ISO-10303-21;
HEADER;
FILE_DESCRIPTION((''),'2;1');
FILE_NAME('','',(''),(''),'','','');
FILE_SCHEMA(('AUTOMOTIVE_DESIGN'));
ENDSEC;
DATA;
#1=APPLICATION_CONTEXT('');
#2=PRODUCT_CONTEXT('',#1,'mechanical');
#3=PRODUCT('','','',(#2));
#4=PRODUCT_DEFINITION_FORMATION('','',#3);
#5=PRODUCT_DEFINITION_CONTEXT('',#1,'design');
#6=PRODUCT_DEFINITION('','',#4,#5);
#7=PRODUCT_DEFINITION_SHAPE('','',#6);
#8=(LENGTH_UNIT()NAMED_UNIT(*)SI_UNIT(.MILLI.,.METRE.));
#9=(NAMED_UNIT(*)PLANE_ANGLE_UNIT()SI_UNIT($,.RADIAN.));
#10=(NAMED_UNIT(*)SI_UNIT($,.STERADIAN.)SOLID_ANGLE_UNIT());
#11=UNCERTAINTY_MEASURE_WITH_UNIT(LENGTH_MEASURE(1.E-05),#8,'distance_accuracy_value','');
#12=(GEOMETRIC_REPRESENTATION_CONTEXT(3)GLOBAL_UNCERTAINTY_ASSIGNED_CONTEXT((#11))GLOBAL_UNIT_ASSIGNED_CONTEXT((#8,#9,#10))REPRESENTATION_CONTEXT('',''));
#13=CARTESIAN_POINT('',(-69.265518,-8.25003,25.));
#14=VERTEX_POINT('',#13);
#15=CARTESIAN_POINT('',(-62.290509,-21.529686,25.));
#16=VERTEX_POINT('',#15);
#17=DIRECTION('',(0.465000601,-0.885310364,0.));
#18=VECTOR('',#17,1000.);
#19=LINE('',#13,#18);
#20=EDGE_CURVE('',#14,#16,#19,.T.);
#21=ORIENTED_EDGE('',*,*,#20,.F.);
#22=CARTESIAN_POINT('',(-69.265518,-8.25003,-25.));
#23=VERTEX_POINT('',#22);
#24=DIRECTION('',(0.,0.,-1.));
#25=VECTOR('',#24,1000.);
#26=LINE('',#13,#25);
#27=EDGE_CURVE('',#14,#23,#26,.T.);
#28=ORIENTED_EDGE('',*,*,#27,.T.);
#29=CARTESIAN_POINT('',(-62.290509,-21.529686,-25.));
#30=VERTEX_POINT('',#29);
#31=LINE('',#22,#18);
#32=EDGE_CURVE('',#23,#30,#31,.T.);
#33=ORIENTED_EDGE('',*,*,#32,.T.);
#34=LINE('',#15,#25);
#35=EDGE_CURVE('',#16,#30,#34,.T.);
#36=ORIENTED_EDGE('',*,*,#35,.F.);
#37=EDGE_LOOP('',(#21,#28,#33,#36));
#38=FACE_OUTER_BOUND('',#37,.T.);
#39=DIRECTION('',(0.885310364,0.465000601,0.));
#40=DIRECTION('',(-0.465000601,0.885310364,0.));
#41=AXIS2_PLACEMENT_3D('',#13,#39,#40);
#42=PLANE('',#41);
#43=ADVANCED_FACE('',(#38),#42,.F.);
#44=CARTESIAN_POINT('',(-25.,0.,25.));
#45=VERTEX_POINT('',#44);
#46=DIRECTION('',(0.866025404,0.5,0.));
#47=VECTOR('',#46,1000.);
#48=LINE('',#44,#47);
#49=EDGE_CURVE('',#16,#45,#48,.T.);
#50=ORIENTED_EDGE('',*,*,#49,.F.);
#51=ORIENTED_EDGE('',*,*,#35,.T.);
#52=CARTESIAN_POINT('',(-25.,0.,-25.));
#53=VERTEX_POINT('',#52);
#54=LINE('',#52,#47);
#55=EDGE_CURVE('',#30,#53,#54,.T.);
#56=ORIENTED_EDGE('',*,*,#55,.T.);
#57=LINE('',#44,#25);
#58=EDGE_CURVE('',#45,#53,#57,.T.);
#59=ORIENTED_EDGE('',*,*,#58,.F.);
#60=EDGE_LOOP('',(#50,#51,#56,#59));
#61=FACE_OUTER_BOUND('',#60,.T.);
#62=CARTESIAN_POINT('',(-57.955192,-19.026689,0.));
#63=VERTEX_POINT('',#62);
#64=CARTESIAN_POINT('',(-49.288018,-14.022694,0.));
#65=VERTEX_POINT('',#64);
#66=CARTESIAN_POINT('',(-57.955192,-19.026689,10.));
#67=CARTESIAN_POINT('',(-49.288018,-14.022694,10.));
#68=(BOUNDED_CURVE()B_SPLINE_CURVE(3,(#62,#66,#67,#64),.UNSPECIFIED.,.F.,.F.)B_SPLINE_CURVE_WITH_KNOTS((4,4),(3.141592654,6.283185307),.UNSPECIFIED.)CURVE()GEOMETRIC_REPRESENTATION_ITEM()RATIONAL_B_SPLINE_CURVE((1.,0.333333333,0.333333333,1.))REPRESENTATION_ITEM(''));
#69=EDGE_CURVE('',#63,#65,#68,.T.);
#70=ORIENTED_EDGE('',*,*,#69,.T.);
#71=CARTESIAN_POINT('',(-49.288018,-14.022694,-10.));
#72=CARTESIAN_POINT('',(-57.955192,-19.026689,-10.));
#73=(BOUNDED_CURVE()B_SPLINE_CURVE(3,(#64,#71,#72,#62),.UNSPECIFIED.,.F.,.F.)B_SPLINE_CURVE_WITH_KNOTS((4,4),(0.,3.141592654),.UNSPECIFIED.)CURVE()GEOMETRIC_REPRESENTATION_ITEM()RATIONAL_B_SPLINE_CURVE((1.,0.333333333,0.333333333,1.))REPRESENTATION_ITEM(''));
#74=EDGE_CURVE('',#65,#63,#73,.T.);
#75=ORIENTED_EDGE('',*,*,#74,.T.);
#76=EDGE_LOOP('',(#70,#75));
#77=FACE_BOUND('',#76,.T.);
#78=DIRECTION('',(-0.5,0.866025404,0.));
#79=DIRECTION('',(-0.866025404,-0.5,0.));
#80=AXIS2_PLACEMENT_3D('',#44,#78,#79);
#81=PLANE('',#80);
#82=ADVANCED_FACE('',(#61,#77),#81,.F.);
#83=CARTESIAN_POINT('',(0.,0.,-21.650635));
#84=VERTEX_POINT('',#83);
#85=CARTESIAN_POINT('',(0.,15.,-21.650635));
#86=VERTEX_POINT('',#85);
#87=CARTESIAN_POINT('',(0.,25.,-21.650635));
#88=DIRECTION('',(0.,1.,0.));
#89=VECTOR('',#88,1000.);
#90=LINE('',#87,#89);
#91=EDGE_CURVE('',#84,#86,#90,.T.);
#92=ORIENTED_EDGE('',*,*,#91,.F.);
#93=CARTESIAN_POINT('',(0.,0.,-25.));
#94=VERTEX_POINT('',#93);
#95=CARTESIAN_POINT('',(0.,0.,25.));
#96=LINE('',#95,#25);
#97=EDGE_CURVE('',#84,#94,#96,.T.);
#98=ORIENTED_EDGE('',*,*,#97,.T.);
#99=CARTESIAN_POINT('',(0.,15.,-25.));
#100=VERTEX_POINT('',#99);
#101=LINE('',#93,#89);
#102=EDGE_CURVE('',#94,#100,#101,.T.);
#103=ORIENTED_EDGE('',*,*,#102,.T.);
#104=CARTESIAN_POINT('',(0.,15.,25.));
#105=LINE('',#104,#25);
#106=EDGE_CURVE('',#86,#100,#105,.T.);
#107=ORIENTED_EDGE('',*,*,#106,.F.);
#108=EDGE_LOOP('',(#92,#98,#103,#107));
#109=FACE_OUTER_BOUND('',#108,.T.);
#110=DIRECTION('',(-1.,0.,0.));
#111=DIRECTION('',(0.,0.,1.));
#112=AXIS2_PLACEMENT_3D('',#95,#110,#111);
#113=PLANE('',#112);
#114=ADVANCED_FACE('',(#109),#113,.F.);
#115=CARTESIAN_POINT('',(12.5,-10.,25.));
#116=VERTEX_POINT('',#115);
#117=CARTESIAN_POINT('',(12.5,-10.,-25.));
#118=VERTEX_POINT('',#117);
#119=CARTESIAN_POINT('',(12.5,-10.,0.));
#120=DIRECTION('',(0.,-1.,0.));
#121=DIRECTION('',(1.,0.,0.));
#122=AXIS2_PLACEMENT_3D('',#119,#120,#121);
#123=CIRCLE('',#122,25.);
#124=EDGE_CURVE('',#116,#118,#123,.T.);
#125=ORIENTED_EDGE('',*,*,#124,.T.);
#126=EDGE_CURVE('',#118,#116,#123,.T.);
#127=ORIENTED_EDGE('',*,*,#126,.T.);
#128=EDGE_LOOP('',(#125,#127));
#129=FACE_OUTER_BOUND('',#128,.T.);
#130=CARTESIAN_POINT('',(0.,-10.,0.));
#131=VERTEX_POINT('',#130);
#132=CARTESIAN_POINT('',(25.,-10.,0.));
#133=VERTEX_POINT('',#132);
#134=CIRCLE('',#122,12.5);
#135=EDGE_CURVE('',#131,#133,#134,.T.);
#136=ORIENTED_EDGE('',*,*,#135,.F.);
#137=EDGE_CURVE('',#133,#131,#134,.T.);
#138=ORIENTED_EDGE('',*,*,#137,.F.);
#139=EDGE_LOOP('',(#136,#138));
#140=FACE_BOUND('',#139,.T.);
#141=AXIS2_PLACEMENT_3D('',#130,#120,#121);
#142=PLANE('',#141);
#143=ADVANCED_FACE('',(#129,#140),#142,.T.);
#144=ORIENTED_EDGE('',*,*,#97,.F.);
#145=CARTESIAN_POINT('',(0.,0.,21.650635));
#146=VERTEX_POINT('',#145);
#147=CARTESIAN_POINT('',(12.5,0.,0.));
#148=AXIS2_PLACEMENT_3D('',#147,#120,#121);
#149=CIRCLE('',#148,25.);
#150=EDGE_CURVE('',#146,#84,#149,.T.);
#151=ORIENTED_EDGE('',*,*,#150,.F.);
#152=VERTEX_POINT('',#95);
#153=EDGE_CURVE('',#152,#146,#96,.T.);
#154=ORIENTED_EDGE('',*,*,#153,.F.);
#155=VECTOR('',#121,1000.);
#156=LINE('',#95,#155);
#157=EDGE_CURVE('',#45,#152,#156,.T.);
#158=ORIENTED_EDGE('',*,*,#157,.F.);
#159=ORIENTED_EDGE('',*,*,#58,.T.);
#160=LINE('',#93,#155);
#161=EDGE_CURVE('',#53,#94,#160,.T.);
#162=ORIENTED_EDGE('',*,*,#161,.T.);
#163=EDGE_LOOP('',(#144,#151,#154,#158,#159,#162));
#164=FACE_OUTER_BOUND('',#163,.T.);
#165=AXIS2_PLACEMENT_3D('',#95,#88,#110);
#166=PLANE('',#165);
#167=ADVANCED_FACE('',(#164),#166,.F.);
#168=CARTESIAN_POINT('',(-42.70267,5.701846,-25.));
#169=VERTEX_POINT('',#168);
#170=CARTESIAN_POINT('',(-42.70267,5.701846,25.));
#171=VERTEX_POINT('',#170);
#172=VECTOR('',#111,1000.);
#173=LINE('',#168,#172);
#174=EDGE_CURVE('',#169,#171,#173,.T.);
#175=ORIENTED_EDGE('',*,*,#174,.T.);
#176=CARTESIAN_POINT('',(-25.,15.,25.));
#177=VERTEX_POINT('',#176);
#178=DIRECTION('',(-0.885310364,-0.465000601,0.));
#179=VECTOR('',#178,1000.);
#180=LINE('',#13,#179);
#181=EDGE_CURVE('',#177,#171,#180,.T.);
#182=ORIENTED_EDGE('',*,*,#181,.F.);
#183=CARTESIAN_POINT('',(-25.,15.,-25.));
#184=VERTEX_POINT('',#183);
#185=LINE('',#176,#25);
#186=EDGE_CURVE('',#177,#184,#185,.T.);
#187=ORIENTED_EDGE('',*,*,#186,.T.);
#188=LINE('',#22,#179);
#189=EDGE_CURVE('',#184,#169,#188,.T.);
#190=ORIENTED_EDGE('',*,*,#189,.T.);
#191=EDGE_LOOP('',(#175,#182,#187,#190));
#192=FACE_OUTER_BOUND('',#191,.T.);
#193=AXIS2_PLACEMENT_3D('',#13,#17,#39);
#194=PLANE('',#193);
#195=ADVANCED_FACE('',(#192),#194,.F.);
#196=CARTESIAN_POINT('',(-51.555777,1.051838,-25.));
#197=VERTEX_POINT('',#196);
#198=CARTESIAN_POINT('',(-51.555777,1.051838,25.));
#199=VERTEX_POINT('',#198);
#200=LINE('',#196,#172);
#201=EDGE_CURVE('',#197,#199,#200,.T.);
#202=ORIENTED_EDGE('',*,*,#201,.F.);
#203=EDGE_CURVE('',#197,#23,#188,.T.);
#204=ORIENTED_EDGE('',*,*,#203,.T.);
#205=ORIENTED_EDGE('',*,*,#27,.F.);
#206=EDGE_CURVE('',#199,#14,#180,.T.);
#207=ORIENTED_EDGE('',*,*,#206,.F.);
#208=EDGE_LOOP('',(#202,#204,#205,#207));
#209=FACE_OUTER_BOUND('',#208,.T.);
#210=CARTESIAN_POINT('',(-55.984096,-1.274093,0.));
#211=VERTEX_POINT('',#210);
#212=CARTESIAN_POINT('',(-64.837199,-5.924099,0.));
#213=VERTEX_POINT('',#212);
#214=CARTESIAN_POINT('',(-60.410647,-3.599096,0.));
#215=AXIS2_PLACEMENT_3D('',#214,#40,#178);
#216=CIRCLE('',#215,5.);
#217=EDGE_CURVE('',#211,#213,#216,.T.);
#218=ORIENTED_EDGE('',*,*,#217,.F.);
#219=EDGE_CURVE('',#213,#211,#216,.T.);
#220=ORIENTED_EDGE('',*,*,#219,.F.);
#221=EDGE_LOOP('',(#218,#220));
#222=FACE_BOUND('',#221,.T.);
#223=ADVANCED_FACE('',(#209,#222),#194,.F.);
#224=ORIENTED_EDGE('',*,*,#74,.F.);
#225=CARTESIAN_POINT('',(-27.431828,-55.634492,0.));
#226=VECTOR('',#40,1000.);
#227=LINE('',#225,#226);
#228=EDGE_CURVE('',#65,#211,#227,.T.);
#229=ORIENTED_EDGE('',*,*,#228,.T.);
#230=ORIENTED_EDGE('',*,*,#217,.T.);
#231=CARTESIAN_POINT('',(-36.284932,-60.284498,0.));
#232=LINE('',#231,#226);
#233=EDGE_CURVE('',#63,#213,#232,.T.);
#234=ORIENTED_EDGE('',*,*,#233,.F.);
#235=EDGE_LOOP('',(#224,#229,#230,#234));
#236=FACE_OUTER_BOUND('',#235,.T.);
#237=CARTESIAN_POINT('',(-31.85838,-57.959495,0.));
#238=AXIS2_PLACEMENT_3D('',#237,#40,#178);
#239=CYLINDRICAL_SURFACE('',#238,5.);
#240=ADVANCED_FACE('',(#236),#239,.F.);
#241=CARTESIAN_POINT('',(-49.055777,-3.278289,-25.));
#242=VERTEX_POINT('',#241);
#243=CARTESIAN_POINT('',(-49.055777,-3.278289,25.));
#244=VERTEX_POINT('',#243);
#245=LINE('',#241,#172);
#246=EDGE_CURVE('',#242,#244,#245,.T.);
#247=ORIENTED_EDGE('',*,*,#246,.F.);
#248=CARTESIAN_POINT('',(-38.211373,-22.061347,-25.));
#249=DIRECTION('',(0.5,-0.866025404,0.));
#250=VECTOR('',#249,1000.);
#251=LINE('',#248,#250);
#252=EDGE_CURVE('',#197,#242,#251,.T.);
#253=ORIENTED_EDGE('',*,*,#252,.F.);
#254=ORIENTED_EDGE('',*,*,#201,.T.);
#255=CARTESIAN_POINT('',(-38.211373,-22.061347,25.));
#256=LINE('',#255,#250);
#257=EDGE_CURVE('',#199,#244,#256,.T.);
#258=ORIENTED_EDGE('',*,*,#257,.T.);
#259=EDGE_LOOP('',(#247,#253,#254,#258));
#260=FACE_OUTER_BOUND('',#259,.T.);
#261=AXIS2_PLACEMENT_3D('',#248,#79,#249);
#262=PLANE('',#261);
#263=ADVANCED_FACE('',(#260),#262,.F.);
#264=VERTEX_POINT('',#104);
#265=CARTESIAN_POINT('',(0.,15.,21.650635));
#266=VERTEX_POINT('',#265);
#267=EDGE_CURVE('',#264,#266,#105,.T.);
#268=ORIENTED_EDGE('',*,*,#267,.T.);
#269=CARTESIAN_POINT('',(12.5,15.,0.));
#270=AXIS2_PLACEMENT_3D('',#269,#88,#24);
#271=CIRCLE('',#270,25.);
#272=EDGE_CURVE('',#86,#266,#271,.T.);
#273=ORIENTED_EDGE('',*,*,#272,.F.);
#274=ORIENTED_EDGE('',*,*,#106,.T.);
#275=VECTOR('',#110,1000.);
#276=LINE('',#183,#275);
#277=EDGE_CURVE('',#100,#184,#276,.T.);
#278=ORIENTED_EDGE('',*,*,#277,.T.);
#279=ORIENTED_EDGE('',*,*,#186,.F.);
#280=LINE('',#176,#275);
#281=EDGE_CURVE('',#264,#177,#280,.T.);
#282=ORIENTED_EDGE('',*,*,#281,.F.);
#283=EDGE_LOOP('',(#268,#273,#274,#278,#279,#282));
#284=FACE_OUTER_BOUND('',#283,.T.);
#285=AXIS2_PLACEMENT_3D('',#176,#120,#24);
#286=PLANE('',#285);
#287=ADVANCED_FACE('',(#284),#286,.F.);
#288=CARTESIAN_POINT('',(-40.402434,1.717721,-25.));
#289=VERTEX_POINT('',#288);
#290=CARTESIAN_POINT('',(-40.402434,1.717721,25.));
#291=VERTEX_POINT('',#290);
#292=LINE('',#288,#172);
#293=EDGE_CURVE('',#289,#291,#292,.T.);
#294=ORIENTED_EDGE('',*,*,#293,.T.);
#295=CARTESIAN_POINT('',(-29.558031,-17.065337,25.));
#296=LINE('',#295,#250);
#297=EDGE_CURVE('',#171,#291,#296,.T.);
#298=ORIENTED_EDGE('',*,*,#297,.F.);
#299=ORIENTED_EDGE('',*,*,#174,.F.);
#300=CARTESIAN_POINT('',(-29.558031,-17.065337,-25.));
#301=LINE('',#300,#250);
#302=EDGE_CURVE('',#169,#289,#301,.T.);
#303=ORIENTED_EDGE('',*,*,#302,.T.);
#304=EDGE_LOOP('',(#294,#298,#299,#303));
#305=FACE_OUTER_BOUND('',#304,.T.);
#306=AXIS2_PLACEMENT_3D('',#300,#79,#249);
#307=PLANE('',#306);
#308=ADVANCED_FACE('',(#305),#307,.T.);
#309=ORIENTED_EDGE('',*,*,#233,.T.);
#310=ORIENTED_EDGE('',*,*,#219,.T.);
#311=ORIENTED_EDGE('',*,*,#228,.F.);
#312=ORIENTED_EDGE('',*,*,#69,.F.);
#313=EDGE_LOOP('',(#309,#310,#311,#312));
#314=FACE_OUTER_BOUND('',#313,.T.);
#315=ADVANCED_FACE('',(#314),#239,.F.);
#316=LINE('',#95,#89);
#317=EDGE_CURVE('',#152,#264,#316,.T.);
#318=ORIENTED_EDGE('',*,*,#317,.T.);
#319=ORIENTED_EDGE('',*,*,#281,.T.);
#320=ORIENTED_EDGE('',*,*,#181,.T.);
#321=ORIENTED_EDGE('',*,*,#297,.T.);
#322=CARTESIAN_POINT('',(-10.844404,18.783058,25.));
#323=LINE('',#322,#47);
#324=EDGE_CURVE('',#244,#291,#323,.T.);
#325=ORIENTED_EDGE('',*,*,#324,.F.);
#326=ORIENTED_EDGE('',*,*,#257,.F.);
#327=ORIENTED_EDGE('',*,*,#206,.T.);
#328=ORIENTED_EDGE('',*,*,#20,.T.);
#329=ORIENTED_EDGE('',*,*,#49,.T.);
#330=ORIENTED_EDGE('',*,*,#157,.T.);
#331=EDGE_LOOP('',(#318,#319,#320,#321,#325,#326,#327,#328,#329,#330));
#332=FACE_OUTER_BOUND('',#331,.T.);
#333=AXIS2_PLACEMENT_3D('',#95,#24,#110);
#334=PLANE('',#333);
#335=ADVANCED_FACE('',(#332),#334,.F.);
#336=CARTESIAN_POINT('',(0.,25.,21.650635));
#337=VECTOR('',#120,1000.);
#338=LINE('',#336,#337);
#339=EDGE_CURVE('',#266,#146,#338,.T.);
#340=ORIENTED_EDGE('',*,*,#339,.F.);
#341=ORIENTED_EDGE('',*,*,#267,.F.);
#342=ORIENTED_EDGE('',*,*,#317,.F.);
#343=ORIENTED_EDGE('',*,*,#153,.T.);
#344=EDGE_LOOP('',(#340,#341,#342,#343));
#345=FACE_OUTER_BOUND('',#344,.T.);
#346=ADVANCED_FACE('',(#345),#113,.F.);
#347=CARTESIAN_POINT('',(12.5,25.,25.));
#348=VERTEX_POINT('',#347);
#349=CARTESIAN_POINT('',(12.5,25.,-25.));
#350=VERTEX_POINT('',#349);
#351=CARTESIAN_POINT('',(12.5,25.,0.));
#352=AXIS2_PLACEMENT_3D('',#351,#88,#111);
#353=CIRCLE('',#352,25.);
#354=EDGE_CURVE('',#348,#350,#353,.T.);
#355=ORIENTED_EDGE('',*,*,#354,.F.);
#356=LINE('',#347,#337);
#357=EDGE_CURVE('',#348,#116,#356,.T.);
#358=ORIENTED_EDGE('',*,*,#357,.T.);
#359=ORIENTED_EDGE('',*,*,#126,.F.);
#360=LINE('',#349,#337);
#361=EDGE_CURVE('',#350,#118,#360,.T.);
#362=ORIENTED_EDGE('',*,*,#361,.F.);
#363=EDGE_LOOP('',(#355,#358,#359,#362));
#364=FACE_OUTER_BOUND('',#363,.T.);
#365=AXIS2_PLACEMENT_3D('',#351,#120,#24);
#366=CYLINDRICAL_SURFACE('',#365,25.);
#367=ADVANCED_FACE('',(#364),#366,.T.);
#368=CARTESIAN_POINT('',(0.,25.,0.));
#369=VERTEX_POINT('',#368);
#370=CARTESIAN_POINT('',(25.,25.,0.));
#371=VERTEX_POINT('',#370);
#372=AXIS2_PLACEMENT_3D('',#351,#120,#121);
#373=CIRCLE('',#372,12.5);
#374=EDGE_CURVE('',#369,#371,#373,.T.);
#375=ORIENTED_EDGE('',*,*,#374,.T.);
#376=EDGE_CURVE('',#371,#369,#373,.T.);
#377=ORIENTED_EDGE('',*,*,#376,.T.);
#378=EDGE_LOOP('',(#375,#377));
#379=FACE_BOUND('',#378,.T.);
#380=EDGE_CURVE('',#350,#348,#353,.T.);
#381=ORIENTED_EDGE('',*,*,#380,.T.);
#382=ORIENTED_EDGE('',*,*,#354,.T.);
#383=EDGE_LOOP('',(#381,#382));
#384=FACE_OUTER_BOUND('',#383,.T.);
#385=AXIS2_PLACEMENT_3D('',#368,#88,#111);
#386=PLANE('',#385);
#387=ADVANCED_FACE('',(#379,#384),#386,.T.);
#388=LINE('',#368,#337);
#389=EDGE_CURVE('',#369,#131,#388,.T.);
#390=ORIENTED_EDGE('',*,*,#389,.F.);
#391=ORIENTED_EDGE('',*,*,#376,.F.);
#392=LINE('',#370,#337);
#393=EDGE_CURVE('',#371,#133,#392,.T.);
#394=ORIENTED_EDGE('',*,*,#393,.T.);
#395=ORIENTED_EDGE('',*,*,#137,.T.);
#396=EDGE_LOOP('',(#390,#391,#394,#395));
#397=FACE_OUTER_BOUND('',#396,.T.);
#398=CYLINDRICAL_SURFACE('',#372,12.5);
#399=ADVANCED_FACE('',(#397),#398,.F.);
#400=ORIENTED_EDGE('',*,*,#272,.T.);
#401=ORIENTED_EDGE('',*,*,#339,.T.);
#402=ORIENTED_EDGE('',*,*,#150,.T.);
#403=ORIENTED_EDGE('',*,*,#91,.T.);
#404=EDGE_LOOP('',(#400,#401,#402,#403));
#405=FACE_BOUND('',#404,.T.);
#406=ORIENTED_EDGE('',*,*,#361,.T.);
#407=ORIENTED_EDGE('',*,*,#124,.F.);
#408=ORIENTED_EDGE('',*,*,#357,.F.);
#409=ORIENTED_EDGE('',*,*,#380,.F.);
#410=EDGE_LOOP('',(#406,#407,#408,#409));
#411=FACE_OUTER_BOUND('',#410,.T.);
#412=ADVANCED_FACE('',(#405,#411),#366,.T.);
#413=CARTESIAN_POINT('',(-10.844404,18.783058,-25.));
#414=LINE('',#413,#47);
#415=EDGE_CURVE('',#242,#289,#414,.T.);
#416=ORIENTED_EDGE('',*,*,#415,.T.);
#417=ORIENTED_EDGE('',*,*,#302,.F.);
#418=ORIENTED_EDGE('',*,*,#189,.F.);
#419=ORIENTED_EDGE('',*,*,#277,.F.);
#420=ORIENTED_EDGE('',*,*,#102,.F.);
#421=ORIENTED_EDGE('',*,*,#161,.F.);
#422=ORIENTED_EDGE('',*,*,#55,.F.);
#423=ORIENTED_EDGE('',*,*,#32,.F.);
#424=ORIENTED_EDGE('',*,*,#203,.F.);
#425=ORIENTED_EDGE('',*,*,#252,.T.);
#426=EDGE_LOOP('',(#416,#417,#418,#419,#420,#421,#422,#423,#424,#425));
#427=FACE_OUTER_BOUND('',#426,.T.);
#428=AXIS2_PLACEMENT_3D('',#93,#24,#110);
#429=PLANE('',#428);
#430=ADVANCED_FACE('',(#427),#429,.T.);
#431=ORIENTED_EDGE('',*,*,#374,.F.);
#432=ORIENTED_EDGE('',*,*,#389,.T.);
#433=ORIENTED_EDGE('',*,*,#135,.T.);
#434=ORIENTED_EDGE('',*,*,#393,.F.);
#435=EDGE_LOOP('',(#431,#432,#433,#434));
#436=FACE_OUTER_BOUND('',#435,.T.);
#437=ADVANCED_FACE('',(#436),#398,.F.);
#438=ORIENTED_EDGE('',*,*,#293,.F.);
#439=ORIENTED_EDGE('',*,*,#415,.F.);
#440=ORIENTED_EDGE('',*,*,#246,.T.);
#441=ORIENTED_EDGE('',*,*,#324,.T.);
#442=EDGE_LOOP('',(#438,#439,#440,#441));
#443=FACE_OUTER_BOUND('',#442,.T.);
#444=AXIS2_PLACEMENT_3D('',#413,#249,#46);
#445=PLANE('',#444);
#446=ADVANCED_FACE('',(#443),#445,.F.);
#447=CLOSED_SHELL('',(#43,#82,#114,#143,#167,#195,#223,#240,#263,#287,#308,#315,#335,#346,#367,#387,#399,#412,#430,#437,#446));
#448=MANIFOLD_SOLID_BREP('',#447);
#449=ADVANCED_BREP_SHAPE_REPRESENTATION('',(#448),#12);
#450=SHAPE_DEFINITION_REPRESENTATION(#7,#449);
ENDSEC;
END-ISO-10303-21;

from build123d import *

# Parameters (mm, degrees)
BASE_BLOCK_DEPTH       = 25
CYLINDER_BOSS_SKETCH_R = 25
CYLINDER_BOSS_50_DEPTH = 25
WEB_START              = 10
WEB_BOSS_DEPTH         = 10
BORE_SKETCH_R          = 12.5
BORE_25_DEPTH          = 82.533502
T_SLOT_CUT_DEPTH       = 90.009618
HOLE_SKETCH_R          = 5
HOLE_10_DEPTH          = 77.495661


with BuildPart() as part:
    # Base Profile Sketch → Base Block (new, symmetric)
    with BuildSketch(Plane.XY):
        Polygon((0, 0), (-25, 0), (-62.290509, -21.529686), (-69.265518, -8.25003), (-25, 15), (0, 15), align=None)
    extrude(amount=BASE_BLOCK_DEPTH, both=True)

    # Cylinder Boss Sketch → Cylinder Boss Ø50 (add)
    with BuildSketch(Plane(origin=(0, 0, 0), x_dir=(1, 0, 0), z_dir=(0, 1, 0))):
        with Locations(Location((12.5, 0, 0), (0, 0, 120))):
            Circle(CYLINDER_BOSS_SKETCH_R)
    extrude(amount=CYLINDER_BOSS_50_DEPTH)

    # Web Boss Sketch → Web Boss (add)
    with BuildSketch(Plane.XZ.offset(WEB_START)):
        with BuildLine():
            ThreePointArc((0, 21.650635), (-12.5, 0), (0, -21.650635))
            ThreePointArc((0, -21.650635), (25, -21.650635), (37.5, 0))
            ThreePointArc((37.5, 0), (25, 21.650635), (0, 21.650635))
        make_face()
    extrude(amount=-WEB_BOSS_DEPTH)

    # Bore Sketch → Bore Ø25 (cut, through all)
    with BuildSketch(Plane.XZ.offset(10)):
        with Locations((12.5, 0)):
            Circle(BORE_SKETCH_R)
    extrude(amount=-BORE_25_DEPTH, mode=Mode.SUBTRACT)

    # T-Slot Sketch → T-Slot Cut (cut, through all)
    with BuildSketch(Plane.XY.offset(25)):
        Polygon((-42.70267, 5.701846), (-51.555777, 1.051838), (-49.055777, -3.278289), (-40.402434, 1.717721), align=None)
    extrude(amount=-T_SLOT_CUT_DEPTH, mode=Mode.SUBTRACT)

    # Hole Sketch → Hole Ø10 (cut, through all)
    with BuildSketch(Plane(origin=(-11.580687, 22.048363, 0), x_dir=(0.8853103641838149, 0.4650006011487738, 0), z_dir=(-0.4650006011487738, 0.8853103641838149, 0))):
        with Locations(Location((-55.155754, 0, 0), (0, 0, 180))):
            Circle(HOLE_SKETCH_R)
    extrude(amount=-HOLE_10_DEPTH, mode=Mode.SUBTRACT)


solid = part.part
